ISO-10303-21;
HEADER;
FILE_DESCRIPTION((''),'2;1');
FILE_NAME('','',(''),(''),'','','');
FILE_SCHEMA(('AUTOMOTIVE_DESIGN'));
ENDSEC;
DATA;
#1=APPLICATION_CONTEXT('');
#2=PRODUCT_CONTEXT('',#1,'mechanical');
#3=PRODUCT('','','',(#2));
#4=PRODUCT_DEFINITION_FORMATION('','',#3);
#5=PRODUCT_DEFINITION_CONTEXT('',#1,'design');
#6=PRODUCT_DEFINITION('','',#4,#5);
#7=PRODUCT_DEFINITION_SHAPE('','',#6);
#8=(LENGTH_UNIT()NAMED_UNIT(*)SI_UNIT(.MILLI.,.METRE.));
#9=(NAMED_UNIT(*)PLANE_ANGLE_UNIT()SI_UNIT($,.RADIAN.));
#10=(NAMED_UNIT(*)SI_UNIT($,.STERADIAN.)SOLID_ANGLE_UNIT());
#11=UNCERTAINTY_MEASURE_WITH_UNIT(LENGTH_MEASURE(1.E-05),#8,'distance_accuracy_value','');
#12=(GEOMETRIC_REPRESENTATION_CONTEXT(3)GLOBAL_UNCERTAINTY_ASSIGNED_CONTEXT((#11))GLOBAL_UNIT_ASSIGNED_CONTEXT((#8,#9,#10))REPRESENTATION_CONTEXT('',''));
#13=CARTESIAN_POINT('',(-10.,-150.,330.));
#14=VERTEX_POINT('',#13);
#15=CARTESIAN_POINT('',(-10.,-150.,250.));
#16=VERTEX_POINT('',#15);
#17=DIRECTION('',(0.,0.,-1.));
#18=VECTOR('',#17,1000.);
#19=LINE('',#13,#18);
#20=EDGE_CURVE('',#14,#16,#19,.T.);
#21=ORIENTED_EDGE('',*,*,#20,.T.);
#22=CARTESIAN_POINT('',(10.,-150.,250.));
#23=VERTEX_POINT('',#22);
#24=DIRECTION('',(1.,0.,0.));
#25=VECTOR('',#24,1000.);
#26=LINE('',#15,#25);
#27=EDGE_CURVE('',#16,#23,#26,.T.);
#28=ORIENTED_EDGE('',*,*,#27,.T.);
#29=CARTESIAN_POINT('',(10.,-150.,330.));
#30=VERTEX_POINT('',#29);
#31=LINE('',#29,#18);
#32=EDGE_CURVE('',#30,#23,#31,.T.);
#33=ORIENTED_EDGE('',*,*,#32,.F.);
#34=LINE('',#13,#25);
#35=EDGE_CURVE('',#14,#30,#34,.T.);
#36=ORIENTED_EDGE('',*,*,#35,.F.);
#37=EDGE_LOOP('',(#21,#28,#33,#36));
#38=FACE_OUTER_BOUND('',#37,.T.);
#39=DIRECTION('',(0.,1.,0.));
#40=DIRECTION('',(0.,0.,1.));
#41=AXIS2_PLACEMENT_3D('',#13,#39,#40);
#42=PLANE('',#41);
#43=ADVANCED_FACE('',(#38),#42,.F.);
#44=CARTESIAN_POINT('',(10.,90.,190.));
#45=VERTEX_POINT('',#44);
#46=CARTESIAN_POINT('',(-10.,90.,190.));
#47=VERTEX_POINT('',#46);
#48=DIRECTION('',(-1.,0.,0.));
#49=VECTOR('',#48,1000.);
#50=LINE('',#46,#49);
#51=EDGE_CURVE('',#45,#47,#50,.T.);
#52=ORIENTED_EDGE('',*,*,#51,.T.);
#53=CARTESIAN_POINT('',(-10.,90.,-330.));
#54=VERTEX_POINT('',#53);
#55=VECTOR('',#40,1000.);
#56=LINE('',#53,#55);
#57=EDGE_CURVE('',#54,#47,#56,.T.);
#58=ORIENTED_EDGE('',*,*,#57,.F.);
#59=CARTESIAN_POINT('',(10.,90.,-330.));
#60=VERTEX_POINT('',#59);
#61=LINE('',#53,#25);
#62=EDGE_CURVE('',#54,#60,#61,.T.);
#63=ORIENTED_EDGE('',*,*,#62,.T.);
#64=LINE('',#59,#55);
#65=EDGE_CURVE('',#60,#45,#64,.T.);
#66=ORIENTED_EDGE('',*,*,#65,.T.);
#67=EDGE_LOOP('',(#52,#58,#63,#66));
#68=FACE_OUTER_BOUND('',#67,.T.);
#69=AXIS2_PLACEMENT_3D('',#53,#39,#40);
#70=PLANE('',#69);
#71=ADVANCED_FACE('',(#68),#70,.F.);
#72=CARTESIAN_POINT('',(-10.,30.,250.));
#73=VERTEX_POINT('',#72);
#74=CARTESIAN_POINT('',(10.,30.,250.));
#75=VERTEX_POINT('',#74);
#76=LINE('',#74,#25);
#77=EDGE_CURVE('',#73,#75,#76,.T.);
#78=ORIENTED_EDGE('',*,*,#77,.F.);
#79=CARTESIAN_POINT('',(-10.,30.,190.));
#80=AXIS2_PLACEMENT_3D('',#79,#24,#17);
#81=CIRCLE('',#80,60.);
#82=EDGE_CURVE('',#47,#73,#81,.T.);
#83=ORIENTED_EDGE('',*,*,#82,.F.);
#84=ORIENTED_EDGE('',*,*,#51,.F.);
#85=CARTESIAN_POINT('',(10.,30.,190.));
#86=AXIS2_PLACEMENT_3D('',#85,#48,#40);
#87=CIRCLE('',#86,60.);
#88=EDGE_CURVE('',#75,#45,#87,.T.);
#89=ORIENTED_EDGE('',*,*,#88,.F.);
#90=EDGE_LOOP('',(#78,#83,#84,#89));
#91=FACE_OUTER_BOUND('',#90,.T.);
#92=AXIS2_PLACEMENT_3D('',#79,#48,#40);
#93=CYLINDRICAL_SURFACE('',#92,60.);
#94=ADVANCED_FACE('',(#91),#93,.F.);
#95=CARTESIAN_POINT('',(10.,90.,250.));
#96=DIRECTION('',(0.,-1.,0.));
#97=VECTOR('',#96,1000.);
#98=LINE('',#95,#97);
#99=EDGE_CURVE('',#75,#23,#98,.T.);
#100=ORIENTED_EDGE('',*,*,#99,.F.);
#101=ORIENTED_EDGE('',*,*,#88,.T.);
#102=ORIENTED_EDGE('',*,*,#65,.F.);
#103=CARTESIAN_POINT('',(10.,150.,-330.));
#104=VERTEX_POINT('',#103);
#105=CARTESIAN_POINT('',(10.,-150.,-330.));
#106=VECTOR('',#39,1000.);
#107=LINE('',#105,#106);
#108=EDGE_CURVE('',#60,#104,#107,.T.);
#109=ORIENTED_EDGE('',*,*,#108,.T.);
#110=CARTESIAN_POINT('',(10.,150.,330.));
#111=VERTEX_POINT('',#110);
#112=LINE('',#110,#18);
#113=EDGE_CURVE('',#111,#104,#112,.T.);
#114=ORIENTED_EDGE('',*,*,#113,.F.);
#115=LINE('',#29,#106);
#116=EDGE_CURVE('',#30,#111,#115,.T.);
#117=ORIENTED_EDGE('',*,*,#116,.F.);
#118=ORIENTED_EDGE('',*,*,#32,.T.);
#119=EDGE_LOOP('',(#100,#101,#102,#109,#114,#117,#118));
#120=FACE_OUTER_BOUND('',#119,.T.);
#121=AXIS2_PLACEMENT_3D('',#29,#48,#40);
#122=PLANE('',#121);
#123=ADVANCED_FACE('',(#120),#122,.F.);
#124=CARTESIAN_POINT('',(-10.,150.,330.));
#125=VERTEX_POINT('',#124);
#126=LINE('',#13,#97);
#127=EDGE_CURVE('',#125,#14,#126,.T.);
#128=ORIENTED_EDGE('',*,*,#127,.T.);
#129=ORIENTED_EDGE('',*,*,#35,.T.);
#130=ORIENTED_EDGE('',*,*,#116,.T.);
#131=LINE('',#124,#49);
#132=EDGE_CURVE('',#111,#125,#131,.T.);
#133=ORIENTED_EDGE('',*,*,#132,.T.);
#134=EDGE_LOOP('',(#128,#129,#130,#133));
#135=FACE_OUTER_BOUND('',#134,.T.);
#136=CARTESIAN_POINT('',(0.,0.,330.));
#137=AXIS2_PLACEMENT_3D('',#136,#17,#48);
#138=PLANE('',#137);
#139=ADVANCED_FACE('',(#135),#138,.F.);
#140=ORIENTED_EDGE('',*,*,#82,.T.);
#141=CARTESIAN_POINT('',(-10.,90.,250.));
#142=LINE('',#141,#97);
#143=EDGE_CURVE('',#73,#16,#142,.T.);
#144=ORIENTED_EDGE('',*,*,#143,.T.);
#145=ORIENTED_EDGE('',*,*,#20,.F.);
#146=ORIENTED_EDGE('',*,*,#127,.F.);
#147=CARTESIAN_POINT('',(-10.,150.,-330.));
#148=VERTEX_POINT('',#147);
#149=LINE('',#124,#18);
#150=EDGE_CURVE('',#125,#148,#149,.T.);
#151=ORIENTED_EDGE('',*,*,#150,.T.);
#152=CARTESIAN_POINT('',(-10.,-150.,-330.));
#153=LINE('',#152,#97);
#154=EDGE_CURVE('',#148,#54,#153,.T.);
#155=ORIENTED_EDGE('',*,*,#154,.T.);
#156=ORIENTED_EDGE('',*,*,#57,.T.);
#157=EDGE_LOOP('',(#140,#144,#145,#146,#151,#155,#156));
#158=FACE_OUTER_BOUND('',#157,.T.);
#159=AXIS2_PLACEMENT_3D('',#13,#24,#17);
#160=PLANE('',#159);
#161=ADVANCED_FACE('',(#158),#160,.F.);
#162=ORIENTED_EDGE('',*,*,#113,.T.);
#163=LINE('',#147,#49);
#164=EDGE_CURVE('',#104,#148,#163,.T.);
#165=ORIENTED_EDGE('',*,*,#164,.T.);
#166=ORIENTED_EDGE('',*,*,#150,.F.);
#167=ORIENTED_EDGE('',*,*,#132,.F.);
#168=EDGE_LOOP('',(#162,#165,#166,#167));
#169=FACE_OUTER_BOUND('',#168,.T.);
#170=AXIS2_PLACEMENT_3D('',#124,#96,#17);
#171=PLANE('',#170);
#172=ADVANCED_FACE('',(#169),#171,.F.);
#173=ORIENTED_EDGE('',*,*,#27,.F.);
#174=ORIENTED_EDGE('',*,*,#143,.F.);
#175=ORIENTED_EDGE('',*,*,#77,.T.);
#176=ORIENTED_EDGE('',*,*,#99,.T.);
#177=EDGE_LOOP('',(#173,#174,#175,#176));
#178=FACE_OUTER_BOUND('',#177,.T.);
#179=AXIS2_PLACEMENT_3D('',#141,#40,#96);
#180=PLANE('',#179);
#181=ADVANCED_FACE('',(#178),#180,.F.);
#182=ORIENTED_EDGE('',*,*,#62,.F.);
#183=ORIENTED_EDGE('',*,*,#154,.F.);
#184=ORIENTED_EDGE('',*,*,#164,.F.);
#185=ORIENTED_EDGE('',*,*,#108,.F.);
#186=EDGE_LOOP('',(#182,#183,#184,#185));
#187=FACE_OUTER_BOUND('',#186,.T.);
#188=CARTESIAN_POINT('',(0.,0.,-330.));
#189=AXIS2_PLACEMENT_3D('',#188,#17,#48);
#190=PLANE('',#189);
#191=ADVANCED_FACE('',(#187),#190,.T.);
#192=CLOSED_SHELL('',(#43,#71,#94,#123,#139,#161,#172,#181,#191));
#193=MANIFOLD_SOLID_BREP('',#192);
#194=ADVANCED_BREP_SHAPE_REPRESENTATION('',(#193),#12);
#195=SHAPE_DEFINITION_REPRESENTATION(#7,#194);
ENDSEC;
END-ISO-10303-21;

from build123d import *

# Parameters (mm, degrees)
SKETCH_1_W          = 20
SKETCH_1_H          = 300
EXTRUDE_1_DEPTH     = 330
SKETCH_2_W          = 580
SKETCH_2_H          = 240
CUT_EXTRUDE_1_DEPTH = 364.042697213
FILLET_1_R          = 60


with BuildPart() as part:
    # 草图1 → 凸台-拉伸1 (new, symmetric)
    with BuildSketch(Plane.XY):
        Rectangle(SKETCH_1_W, SKETCH_1_H)
    extrude(amount=EXTRUDE_1_DEPTH, both=True)

    # 草图2 → 切除-拉伸1 (cut, through all)
    with BuildSketch(Plane(origin=(10, 0, 0), x_dir=(0, 0, -1), z_dir=(1, 0, 0))):
        with Locations((40, -30)):
            Rectangle(SKETCH_2_W, SKETCH_2_H)
    extrude(amount=-CUT_EXTRUDE_1_DEPTH, mode=Mode.SUBTRACT)

    # 圆角1
    fillet_1_edges = [part.edges().sort_by_distance(p)[0] for p in [
        (0, 90, 250),
    ]]
    fillet(fillet_1_edges, radius=FILLET_1_R)


solid = part.part
